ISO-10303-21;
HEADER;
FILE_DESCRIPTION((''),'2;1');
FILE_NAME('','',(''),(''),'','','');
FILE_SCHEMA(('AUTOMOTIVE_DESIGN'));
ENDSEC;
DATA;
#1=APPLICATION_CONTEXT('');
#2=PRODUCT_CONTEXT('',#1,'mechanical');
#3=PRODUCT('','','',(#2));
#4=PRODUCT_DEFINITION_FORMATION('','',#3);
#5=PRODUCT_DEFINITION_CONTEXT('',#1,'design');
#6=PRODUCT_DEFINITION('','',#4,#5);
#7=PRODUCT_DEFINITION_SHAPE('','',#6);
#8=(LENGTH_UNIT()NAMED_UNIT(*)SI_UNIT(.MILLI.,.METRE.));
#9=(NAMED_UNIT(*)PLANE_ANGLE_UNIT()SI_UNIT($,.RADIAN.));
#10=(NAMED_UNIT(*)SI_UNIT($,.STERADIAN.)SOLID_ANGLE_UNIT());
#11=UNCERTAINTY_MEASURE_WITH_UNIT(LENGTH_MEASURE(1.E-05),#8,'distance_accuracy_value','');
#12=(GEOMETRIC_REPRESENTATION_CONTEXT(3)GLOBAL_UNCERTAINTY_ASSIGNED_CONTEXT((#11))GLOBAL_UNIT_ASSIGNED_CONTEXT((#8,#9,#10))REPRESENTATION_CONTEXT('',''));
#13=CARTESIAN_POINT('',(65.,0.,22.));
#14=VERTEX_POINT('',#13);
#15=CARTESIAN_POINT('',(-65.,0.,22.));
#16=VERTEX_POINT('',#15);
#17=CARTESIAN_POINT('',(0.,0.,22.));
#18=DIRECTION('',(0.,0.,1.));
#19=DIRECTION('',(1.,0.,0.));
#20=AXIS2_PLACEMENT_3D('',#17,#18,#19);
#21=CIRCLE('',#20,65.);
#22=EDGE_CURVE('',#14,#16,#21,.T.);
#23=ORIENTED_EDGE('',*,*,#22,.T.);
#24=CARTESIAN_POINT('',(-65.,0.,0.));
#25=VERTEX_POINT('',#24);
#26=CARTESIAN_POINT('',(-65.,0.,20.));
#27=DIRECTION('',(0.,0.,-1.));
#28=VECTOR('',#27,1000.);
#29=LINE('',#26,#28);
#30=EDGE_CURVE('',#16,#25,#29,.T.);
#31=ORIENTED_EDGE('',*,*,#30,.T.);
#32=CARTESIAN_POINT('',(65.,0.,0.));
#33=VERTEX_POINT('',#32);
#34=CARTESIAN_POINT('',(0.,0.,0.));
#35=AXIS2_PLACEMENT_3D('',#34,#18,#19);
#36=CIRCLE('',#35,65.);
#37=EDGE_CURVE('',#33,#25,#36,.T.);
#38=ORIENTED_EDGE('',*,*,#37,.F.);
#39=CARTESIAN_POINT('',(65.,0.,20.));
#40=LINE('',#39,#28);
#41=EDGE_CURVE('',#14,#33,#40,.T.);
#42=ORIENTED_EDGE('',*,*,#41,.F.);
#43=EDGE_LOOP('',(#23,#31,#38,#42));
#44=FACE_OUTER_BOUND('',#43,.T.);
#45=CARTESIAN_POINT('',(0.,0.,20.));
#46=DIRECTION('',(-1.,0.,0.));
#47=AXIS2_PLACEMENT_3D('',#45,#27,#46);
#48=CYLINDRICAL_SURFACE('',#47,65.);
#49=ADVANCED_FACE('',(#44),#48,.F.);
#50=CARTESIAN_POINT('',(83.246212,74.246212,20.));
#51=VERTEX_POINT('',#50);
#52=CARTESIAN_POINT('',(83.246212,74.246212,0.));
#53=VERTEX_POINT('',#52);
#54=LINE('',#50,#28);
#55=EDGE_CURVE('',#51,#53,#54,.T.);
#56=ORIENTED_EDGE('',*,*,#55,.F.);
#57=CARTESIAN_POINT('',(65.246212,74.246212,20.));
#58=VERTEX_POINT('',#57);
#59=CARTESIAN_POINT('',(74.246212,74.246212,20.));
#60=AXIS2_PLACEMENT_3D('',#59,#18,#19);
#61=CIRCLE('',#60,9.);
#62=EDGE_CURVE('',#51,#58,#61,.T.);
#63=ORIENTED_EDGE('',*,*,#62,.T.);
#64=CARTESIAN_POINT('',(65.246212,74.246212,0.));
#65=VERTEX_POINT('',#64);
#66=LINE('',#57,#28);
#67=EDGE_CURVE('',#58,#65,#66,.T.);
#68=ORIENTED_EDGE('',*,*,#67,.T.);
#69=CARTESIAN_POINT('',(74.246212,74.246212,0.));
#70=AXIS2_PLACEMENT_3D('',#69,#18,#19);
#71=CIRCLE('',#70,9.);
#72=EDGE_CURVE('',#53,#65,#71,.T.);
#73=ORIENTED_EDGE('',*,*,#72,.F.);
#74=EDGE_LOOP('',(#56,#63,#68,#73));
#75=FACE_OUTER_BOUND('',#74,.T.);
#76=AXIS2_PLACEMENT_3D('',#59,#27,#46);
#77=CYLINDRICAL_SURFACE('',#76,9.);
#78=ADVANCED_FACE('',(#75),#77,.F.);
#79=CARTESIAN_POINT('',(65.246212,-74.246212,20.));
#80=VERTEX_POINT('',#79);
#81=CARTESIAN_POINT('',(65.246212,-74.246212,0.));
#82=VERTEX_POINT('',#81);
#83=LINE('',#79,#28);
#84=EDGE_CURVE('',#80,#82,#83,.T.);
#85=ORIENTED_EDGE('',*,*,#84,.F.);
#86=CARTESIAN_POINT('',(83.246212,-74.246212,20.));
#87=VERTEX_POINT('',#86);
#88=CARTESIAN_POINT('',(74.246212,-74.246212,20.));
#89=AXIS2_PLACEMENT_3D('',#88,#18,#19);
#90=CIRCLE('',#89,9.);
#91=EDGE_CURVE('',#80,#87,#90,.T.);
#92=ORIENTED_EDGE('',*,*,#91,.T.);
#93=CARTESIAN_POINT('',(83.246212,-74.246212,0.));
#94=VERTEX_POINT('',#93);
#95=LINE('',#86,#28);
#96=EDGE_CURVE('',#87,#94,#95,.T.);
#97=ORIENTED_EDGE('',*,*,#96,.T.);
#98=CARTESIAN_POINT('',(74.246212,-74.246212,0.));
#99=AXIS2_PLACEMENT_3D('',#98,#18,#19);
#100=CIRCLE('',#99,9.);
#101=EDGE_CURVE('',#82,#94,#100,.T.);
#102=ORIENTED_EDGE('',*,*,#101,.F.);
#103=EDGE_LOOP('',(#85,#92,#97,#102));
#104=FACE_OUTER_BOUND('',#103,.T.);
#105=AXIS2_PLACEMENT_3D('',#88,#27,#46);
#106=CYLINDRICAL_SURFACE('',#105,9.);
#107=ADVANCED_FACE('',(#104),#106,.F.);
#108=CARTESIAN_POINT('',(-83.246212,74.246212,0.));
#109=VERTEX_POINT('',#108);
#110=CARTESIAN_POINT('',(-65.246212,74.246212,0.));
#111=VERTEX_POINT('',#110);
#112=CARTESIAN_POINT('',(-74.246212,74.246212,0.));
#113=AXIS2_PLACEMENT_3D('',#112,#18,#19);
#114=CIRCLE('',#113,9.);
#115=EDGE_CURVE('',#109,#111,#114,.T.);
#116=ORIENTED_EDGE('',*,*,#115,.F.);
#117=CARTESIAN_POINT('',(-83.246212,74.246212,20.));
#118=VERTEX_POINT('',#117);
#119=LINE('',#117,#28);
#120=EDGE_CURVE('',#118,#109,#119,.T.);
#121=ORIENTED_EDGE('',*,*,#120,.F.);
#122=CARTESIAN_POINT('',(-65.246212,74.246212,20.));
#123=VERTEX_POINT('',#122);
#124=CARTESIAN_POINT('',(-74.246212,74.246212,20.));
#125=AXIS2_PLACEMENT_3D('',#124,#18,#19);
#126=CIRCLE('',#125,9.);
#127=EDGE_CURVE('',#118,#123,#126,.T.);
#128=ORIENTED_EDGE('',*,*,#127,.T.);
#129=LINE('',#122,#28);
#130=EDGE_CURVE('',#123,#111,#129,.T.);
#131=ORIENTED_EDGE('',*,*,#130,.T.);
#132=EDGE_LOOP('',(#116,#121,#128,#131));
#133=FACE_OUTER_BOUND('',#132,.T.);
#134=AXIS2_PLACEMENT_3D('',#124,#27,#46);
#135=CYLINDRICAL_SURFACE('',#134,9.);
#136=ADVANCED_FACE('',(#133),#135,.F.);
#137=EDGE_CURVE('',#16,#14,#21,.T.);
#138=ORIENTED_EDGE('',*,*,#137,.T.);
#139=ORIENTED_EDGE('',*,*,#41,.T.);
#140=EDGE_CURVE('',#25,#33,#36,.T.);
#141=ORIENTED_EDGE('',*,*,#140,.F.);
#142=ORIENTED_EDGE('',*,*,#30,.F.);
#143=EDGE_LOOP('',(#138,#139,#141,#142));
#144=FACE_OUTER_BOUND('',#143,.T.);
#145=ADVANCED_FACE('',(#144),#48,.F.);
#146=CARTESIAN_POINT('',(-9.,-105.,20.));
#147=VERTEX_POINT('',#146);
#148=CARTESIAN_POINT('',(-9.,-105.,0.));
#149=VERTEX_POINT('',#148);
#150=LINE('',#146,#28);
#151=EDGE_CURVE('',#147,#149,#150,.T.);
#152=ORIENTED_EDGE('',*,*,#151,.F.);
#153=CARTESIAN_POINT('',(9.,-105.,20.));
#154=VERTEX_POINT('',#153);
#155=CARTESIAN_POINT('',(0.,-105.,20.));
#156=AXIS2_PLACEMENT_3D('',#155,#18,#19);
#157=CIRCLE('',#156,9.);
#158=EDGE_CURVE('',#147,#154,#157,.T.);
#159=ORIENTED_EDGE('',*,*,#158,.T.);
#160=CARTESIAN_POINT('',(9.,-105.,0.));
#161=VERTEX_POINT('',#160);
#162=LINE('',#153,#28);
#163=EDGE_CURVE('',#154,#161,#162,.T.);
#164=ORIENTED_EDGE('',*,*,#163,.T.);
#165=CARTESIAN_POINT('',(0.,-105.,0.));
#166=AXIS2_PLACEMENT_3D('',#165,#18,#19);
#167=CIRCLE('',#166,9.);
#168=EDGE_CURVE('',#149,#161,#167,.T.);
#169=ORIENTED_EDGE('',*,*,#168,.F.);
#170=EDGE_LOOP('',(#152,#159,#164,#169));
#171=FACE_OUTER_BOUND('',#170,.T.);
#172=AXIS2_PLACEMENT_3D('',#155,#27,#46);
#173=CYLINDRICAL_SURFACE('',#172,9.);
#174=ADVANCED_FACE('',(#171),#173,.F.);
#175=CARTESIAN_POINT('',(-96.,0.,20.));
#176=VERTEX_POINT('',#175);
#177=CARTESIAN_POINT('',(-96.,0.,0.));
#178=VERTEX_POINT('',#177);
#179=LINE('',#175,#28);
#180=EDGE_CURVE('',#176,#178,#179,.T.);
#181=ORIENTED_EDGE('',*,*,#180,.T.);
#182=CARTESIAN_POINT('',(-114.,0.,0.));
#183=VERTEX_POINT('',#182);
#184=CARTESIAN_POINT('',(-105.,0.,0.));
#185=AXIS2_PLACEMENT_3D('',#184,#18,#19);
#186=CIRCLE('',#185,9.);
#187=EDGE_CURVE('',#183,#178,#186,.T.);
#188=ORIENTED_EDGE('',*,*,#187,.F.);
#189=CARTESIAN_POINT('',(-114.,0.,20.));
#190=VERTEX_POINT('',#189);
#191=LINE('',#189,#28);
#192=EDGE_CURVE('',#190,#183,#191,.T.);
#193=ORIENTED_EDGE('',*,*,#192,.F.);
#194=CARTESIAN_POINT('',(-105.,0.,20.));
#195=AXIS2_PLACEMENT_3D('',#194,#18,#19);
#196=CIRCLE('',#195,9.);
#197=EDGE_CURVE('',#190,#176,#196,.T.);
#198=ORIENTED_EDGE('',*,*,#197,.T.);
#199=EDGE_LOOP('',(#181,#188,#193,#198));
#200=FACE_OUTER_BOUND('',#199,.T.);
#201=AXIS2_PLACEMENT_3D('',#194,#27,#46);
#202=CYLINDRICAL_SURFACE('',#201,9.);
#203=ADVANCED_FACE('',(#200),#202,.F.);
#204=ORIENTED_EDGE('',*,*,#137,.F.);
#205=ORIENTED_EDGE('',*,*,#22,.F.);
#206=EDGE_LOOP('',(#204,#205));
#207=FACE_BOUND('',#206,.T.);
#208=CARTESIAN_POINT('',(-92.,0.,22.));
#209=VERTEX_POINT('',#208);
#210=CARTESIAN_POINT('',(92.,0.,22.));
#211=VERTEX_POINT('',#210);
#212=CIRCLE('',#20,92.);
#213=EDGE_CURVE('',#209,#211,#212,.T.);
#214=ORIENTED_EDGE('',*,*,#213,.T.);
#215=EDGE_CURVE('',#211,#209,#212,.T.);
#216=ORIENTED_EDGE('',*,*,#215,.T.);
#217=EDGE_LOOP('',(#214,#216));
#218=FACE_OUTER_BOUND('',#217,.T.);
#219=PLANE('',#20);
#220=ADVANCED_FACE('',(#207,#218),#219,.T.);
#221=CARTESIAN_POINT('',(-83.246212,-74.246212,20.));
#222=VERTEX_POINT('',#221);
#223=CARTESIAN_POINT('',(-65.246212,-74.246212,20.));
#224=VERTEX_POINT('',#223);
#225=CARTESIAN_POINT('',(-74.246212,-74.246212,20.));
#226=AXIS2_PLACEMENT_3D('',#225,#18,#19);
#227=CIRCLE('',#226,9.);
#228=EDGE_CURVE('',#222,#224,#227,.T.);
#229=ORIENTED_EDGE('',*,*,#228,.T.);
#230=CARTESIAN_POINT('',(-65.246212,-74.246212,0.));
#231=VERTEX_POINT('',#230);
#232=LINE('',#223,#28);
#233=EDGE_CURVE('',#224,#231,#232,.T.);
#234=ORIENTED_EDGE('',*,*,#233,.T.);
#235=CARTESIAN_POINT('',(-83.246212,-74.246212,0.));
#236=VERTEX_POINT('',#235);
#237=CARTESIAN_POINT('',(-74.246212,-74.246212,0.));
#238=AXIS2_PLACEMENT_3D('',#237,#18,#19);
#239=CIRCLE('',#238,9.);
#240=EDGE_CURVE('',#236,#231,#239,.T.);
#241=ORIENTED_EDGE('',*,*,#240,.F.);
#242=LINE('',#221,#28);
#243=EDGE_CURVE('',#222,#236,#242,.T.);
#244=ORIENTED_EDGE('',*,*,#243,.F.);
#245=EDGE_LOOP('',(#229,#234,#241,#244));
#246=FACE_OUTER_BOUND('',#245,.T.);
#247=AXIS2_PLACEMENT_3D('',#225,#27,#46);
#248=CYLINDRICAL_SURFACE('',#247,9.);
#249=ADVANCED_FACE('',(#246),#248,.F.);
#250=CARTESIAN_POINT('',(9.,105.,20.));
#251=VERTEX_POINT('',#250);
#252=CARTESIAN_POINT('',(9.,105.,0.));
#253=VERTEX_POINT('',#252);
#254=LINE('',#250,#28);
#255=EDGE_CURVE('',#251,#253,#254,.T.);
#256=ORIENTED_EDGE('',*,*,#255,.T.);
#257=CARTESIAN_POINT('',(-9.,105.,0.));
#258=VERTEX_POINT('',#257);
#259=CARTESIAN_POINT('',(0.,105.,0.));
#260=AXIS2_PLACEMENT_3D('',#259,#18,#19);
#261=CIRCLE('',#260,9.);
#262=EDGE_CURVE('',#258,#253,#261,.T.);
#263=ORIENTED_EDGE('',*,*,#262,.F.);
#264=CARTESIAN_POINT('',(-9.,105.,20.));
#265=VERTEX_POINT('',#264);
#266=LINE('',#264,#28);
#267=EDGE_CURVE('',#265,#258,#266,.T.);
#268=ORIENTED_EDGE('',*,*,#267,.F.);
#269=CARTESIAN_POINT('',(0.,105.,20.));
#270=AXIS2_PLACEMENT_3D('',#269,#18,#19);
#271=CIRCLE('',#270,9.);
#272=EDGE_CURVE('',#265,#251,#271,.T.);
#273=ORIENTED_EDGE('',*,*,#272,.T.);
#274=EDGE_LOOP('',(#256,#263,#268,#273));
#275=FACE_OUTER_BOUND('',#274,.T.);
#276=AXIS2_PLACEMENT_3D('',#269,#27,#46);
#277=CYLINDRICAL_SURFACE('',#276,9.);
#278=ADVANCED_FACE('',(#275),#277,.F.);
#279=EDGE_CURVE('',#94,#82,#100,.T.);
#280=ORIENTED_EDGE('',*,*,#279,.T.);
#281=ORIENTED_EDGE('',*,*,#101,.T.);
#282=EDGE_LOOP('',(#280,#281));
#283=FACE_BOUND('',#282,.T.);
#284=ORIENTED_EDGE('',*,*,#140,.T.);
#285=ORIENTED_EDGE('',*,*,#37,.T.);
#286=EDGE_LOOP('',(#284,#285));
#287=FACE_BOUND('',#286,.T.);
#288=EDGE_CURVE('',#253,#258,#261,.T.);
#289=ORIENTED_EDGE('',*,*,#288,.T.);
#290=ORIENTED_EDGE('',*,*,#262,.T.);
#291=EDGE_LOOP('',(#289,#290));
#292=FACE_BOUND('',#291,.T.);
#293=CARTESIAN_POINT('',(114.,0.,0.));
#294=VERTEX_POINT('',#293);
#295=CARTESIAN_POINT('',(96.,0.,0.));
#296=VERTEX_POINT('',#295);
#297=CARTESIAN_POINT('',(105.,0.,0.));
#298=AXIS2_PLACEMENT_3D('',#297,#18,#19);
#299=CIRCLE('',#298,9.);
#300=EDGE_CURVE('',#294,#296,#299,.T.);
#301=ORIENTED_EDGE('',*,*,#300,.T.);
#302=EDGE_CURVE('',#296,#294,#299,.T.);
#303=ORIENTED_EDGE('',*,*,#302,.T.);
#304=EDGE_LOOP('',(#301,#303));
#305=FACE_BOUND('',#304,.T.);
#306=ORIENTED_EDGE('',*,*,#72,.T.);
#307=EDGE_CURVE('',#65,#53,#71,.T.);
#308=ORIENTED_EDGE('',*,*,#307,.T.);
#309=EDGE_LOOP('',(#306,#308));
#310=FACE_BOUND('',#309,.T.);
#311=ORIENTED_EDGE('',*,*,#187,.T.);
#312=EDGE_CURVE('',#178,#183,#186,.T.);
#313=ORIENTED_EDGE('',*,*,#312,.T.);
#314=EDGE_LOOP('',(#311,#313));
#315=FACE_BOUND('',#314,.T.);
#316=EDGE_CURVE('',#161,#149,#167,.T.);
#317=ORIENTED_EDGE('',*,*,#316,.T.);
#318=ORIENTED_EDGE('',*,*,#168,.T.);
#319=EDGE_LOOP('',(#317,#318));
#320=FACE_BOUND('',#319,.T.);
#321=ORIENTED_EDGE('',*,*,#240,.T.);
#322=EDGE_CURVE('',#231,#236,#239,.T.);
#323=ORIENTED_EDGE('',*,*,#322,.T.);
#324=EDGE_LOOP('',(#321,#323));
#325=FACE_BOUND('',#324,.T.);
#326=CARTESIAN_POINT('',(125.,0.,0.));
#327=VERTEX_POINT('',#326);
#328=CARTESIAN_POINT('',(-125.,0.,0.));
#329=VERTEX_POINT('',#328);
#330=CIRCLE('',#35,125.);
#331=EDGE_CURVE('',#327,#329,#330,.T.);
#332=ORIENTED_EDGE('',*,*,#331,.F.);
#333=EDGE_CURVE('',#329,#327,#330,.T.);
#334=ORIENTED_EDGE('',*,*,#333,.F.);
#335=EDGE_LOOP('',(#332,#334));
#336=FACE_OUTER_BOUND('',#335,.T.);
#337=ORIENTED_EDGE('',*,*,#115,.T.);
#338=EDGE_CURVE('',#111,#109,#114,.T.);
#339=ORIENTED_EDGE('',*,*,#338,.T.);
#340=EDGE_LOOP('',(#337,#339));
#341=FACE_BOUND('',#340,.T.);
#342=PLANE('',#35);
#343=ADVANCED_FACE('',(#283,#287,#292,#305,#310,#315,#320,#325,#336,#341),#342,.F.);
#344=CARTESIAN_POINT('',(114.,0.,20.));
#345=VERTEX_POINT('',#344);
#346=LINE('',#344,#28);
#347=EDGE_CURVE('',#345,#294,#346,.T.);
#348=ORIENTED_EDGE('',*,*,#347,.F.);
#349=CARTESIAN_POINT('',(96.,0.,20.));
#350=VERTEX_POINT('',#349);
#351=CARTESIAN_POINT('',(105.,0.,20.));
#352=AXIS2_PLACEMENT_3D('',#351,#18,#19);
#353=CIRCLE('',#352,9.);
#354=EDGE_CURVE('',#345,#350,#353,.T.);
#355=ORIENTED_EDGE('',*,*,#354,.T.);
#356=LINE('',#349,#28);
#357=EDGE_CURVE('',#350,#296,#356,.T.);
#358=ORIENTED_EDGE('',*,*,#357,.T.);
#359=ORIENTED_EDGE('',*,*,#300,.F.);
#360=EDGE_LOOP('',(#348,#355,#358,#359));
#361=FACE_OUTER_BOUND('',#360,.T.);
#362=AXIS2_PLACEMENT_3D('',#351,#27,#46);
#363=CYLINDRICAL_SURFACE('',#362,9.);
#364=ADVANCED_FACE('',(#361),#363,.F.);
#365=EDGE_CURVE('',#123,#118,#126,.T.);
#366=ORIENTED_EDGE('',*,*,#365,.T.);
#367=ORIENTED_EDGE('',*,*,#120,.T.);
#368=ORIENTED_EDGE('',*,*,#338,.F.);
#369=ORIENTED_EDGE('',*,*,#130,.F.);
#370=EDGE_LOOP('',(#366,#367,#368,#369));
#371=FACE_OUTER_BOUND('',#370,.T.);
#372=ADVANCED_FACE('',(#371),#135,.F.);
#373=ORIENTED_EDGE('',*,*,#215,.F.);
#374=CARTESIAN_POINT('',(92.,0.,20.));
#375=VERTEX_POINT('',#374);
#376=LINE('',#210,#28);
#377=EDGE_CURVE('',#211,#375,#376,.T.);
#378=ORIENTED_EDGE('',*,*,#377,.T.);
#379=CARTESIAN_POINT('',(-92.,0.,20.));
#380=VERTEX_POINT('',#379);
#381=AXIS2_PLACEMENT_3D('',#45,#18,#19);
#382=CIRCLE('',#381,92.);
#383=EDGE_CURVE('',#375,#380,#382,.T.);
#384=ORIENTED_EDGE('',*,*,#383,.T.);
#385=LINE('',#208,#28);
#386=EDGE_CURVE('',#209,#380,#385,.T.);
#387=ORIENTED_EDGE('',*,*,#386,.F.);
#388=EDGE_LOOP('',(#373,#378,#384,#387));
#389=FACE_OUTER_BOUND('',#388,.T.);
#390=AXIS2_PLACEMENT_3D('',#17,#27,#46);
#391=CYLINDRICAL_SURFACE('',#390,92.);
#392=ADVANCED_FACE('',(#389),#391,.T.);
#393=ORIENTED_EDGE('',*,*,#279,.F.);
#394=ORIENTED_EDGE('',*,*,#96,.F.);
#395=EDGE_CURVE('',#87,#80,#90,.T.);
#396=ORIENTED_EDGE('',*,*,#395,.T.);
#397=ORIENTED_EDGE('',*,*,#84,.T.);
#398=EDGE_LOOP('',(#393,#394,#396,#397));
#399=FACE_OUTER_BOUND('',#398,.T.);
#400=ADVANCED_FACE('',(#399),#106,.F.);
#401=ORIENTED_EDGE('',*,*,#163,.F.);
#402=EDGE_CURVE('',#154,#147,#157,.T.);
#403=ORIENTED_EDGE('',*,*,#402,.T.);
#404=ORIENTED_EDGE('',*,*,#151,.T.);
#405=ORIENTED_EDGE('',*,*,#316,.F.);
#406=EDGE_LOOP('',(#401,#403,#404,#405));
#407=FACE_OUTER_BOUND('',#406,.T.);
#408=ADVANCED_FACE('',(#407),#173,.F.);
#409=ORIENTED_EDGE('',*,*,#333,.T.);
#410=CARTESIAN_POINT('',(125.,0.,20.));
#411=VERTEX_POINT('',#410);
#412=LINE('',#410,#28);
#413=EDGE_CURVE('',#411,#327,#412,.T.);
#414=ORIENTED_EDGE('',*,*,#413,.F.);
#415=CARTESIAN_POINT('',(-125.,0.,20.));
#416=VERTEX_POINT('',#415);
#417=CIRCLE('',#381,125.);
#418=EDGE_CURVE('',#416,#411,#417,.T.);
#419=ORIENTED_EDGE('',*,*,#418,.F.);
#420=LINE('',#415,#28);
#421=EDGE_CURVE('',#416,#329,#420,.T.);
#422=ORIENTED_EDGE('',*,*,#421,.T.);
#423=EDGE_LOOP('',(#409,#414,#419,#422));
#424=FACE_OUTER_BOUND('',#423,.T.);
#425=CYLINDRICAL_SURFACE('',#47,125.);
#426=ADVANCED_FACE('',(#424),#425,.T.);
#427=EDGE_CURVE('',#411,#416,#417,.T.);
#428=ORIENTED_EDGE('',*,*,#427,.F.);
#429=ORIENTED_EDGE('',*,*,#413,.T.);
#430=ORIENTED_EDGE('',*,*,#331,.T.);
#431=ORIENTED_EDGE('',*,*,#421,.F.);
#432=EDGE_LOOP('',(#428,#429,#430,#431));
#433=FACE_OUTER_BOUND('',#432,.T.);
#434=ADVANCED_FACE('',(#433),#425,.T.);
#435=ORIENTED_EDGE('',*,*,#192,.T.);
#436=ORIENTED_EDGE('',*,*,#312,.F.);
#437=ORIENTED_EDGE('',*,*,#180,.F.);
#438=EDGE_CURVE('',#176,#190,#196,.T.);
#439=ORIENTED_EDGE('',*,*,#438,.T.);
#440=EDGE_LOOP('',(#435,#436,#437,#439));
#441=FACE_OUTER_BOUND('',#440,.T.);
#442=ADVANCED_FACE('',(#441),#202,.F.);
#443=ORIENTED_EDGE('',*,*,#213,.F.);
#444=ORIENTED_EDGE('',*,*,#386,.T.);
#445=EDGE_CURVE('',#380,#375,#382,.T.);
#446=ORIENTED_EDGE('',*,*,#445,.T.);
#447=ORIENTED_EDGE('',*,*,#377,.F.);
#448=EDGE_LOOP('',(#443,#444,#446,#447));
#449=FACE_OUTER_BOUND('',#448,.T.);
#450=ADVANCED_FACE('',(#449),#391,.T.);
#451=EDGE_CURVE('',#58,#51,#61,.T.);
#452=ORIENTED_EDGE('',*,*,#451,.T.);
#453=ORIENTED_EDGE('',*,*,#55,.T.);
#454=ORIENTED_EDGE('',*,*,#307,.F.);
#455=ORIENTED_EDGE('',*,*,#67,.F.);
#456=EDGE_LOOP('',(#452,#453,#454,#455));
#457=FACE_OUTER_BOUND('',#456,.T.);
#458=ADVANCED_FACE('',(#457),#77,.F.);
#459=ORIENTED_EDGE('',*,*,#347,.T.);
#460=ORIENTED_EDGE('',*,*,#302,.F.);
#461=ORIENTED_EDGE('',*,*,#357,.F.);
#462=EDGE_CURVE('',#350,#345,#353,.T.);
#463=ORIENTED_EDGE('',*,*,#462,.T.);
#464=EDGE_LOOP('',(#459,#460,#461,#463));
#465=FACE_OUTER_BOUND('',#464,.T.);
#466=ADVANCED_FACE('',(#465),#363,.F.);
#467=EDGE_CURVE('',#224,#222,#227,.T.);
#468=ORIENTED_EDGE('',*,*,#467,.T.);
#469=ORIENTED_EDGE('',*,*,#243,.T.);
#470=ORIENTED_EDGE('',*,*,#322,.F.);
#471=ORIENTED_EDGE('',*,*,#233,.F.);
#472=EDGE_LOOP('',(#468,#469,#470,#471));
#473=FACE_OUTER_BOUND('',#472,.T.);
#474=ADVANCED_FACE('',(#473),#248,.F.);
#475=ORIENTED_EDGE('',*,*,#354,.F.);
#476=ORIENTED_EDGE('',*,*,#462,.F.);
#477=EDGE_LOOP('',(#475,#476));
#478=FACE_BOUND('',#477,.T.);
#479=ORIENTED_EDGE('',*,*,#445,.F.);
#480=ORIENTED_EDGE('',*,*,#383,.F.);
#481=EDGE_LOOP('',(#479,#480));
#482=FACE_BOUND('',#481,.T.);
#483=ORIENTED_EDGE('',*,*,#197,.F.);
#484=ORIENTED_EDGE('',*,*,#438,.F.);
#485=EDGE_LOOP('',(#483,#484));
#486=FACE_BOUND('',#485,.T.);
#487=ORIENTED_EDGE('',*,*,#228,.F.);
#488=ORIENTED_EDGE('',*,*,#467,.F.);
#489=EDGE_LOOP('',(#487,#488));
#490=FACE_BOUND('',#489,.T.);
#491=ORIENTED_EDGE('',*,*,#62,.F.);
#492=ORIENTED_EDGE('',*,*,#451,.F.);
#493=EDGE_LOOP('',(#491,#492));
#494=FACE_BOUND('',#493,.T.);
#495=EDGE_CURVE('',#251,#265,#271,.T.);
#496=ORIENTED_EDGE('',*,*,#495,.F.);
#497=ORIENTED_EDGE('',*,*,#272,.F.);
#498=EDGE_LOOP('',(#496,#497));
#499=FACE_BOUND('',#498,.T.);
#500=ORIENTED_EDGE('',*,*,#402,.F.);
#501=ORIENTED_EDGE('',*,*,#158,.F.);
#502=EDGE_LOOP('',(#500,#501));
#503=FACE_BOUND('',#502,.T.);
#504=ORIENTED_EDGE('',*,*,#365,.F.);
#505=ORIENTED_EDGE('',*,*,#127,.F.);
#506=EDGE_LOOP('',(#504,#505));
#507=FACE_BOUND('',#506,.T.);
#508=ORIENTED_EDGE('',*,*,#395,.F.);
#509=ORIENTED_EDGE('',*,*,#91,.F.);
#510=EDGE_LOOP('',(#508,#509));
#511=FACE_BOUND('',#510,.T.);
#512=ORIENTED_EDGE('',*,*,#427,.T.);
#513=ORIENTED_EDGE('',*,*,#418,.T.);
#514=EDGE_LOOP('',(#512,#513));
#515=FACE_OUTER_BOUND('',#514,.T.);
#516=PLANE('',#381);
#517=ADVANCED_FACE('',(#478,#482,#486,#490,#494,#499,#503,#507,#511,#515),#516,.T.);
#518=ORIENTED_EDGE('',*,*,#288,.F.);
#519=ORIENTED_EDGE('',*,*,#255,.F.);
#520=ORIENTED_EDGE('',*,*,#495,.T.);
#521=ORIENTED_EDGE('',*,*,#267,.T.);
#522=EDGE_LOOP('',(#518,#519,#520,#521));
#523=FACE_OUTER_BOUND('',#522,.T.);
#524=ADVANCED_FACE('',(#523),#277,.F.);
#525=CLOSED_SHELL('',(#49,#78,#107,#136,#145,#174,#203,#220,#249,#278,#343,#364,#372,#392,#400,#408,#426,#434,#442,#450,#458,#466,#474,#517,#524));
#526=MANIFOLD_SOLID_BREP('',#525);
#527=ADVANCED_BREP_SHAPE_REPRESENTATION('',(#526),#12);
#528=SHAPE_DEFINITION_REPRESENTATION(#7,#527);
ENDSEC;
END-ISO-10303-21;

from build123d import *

# Parameters (mm, degrees)
SKETCH1_R           = 125
SKETCH1_R_2         = 65
SKETCH1_R_3         = 9
BOSS_EXTRUDE1_DEPTH = 20
SKETCH2_R           = 92
SKETCH2_R_2         = 65
BOSS_EXTRUDE2_DEPTH = 2


with BuildPart() as part:
    # Sketch1 → Boss-Extrude1 (new body)
    with BuildSketch(Plane.XY):
        Circle(SKETCH1_R)
        Circle(SKETCH1_R_2, mode=Mode.SUBTRACT)
        with Locations((0, 105)):
            Circle(SKETCH1_R_3, mode=Mode.SUBTRACT)
        with Locations((74.246212025, 74.246212025)):
            Circle(SKETCH1_R_3, mode=Mode.SUBTRACT)
        with Locations((105, 0)):
            Circle(SKETCH1_R_3, mode=Mode.SUBTRACT)
        with Locations((74.246212025, -74.246212025)):
            Circle(SKETCH1_R_3, mode=Mode.SUBTRACT)
        with Locations((0, -105)):
            Circle(SKETCH1_R_3, mode=Mode.SUBTRACT)
        with Locations((-74.246212025, -74.246212025)):
            Circle(SKETCH1_R_3, mode=Mode.SUBTRACT)
        with Locations((-105, 0)):
            Circle(SKETCH1_R_3, mode=Mode.SUBTRACT)
        with Locations((-74.246212025, 74.246212025)):
            Circle(SKETCH1_R_3, mode=Mode.SUBTRACT)
    extrude(amount=BOSS_EXTRUDE1_DEPTH)

    # Sketch2 → Boss-Extrude2 (add)
    with BuildSketch(Plane.XY.offset(20)):
        Circle(SKETCH2_R)
        Circle(SKETCH2_R_2, mode=Mode.SUBTRACT)
    extrude(amount=BOSS_EXTRUDE2_DEPTH)


solid = part.part
